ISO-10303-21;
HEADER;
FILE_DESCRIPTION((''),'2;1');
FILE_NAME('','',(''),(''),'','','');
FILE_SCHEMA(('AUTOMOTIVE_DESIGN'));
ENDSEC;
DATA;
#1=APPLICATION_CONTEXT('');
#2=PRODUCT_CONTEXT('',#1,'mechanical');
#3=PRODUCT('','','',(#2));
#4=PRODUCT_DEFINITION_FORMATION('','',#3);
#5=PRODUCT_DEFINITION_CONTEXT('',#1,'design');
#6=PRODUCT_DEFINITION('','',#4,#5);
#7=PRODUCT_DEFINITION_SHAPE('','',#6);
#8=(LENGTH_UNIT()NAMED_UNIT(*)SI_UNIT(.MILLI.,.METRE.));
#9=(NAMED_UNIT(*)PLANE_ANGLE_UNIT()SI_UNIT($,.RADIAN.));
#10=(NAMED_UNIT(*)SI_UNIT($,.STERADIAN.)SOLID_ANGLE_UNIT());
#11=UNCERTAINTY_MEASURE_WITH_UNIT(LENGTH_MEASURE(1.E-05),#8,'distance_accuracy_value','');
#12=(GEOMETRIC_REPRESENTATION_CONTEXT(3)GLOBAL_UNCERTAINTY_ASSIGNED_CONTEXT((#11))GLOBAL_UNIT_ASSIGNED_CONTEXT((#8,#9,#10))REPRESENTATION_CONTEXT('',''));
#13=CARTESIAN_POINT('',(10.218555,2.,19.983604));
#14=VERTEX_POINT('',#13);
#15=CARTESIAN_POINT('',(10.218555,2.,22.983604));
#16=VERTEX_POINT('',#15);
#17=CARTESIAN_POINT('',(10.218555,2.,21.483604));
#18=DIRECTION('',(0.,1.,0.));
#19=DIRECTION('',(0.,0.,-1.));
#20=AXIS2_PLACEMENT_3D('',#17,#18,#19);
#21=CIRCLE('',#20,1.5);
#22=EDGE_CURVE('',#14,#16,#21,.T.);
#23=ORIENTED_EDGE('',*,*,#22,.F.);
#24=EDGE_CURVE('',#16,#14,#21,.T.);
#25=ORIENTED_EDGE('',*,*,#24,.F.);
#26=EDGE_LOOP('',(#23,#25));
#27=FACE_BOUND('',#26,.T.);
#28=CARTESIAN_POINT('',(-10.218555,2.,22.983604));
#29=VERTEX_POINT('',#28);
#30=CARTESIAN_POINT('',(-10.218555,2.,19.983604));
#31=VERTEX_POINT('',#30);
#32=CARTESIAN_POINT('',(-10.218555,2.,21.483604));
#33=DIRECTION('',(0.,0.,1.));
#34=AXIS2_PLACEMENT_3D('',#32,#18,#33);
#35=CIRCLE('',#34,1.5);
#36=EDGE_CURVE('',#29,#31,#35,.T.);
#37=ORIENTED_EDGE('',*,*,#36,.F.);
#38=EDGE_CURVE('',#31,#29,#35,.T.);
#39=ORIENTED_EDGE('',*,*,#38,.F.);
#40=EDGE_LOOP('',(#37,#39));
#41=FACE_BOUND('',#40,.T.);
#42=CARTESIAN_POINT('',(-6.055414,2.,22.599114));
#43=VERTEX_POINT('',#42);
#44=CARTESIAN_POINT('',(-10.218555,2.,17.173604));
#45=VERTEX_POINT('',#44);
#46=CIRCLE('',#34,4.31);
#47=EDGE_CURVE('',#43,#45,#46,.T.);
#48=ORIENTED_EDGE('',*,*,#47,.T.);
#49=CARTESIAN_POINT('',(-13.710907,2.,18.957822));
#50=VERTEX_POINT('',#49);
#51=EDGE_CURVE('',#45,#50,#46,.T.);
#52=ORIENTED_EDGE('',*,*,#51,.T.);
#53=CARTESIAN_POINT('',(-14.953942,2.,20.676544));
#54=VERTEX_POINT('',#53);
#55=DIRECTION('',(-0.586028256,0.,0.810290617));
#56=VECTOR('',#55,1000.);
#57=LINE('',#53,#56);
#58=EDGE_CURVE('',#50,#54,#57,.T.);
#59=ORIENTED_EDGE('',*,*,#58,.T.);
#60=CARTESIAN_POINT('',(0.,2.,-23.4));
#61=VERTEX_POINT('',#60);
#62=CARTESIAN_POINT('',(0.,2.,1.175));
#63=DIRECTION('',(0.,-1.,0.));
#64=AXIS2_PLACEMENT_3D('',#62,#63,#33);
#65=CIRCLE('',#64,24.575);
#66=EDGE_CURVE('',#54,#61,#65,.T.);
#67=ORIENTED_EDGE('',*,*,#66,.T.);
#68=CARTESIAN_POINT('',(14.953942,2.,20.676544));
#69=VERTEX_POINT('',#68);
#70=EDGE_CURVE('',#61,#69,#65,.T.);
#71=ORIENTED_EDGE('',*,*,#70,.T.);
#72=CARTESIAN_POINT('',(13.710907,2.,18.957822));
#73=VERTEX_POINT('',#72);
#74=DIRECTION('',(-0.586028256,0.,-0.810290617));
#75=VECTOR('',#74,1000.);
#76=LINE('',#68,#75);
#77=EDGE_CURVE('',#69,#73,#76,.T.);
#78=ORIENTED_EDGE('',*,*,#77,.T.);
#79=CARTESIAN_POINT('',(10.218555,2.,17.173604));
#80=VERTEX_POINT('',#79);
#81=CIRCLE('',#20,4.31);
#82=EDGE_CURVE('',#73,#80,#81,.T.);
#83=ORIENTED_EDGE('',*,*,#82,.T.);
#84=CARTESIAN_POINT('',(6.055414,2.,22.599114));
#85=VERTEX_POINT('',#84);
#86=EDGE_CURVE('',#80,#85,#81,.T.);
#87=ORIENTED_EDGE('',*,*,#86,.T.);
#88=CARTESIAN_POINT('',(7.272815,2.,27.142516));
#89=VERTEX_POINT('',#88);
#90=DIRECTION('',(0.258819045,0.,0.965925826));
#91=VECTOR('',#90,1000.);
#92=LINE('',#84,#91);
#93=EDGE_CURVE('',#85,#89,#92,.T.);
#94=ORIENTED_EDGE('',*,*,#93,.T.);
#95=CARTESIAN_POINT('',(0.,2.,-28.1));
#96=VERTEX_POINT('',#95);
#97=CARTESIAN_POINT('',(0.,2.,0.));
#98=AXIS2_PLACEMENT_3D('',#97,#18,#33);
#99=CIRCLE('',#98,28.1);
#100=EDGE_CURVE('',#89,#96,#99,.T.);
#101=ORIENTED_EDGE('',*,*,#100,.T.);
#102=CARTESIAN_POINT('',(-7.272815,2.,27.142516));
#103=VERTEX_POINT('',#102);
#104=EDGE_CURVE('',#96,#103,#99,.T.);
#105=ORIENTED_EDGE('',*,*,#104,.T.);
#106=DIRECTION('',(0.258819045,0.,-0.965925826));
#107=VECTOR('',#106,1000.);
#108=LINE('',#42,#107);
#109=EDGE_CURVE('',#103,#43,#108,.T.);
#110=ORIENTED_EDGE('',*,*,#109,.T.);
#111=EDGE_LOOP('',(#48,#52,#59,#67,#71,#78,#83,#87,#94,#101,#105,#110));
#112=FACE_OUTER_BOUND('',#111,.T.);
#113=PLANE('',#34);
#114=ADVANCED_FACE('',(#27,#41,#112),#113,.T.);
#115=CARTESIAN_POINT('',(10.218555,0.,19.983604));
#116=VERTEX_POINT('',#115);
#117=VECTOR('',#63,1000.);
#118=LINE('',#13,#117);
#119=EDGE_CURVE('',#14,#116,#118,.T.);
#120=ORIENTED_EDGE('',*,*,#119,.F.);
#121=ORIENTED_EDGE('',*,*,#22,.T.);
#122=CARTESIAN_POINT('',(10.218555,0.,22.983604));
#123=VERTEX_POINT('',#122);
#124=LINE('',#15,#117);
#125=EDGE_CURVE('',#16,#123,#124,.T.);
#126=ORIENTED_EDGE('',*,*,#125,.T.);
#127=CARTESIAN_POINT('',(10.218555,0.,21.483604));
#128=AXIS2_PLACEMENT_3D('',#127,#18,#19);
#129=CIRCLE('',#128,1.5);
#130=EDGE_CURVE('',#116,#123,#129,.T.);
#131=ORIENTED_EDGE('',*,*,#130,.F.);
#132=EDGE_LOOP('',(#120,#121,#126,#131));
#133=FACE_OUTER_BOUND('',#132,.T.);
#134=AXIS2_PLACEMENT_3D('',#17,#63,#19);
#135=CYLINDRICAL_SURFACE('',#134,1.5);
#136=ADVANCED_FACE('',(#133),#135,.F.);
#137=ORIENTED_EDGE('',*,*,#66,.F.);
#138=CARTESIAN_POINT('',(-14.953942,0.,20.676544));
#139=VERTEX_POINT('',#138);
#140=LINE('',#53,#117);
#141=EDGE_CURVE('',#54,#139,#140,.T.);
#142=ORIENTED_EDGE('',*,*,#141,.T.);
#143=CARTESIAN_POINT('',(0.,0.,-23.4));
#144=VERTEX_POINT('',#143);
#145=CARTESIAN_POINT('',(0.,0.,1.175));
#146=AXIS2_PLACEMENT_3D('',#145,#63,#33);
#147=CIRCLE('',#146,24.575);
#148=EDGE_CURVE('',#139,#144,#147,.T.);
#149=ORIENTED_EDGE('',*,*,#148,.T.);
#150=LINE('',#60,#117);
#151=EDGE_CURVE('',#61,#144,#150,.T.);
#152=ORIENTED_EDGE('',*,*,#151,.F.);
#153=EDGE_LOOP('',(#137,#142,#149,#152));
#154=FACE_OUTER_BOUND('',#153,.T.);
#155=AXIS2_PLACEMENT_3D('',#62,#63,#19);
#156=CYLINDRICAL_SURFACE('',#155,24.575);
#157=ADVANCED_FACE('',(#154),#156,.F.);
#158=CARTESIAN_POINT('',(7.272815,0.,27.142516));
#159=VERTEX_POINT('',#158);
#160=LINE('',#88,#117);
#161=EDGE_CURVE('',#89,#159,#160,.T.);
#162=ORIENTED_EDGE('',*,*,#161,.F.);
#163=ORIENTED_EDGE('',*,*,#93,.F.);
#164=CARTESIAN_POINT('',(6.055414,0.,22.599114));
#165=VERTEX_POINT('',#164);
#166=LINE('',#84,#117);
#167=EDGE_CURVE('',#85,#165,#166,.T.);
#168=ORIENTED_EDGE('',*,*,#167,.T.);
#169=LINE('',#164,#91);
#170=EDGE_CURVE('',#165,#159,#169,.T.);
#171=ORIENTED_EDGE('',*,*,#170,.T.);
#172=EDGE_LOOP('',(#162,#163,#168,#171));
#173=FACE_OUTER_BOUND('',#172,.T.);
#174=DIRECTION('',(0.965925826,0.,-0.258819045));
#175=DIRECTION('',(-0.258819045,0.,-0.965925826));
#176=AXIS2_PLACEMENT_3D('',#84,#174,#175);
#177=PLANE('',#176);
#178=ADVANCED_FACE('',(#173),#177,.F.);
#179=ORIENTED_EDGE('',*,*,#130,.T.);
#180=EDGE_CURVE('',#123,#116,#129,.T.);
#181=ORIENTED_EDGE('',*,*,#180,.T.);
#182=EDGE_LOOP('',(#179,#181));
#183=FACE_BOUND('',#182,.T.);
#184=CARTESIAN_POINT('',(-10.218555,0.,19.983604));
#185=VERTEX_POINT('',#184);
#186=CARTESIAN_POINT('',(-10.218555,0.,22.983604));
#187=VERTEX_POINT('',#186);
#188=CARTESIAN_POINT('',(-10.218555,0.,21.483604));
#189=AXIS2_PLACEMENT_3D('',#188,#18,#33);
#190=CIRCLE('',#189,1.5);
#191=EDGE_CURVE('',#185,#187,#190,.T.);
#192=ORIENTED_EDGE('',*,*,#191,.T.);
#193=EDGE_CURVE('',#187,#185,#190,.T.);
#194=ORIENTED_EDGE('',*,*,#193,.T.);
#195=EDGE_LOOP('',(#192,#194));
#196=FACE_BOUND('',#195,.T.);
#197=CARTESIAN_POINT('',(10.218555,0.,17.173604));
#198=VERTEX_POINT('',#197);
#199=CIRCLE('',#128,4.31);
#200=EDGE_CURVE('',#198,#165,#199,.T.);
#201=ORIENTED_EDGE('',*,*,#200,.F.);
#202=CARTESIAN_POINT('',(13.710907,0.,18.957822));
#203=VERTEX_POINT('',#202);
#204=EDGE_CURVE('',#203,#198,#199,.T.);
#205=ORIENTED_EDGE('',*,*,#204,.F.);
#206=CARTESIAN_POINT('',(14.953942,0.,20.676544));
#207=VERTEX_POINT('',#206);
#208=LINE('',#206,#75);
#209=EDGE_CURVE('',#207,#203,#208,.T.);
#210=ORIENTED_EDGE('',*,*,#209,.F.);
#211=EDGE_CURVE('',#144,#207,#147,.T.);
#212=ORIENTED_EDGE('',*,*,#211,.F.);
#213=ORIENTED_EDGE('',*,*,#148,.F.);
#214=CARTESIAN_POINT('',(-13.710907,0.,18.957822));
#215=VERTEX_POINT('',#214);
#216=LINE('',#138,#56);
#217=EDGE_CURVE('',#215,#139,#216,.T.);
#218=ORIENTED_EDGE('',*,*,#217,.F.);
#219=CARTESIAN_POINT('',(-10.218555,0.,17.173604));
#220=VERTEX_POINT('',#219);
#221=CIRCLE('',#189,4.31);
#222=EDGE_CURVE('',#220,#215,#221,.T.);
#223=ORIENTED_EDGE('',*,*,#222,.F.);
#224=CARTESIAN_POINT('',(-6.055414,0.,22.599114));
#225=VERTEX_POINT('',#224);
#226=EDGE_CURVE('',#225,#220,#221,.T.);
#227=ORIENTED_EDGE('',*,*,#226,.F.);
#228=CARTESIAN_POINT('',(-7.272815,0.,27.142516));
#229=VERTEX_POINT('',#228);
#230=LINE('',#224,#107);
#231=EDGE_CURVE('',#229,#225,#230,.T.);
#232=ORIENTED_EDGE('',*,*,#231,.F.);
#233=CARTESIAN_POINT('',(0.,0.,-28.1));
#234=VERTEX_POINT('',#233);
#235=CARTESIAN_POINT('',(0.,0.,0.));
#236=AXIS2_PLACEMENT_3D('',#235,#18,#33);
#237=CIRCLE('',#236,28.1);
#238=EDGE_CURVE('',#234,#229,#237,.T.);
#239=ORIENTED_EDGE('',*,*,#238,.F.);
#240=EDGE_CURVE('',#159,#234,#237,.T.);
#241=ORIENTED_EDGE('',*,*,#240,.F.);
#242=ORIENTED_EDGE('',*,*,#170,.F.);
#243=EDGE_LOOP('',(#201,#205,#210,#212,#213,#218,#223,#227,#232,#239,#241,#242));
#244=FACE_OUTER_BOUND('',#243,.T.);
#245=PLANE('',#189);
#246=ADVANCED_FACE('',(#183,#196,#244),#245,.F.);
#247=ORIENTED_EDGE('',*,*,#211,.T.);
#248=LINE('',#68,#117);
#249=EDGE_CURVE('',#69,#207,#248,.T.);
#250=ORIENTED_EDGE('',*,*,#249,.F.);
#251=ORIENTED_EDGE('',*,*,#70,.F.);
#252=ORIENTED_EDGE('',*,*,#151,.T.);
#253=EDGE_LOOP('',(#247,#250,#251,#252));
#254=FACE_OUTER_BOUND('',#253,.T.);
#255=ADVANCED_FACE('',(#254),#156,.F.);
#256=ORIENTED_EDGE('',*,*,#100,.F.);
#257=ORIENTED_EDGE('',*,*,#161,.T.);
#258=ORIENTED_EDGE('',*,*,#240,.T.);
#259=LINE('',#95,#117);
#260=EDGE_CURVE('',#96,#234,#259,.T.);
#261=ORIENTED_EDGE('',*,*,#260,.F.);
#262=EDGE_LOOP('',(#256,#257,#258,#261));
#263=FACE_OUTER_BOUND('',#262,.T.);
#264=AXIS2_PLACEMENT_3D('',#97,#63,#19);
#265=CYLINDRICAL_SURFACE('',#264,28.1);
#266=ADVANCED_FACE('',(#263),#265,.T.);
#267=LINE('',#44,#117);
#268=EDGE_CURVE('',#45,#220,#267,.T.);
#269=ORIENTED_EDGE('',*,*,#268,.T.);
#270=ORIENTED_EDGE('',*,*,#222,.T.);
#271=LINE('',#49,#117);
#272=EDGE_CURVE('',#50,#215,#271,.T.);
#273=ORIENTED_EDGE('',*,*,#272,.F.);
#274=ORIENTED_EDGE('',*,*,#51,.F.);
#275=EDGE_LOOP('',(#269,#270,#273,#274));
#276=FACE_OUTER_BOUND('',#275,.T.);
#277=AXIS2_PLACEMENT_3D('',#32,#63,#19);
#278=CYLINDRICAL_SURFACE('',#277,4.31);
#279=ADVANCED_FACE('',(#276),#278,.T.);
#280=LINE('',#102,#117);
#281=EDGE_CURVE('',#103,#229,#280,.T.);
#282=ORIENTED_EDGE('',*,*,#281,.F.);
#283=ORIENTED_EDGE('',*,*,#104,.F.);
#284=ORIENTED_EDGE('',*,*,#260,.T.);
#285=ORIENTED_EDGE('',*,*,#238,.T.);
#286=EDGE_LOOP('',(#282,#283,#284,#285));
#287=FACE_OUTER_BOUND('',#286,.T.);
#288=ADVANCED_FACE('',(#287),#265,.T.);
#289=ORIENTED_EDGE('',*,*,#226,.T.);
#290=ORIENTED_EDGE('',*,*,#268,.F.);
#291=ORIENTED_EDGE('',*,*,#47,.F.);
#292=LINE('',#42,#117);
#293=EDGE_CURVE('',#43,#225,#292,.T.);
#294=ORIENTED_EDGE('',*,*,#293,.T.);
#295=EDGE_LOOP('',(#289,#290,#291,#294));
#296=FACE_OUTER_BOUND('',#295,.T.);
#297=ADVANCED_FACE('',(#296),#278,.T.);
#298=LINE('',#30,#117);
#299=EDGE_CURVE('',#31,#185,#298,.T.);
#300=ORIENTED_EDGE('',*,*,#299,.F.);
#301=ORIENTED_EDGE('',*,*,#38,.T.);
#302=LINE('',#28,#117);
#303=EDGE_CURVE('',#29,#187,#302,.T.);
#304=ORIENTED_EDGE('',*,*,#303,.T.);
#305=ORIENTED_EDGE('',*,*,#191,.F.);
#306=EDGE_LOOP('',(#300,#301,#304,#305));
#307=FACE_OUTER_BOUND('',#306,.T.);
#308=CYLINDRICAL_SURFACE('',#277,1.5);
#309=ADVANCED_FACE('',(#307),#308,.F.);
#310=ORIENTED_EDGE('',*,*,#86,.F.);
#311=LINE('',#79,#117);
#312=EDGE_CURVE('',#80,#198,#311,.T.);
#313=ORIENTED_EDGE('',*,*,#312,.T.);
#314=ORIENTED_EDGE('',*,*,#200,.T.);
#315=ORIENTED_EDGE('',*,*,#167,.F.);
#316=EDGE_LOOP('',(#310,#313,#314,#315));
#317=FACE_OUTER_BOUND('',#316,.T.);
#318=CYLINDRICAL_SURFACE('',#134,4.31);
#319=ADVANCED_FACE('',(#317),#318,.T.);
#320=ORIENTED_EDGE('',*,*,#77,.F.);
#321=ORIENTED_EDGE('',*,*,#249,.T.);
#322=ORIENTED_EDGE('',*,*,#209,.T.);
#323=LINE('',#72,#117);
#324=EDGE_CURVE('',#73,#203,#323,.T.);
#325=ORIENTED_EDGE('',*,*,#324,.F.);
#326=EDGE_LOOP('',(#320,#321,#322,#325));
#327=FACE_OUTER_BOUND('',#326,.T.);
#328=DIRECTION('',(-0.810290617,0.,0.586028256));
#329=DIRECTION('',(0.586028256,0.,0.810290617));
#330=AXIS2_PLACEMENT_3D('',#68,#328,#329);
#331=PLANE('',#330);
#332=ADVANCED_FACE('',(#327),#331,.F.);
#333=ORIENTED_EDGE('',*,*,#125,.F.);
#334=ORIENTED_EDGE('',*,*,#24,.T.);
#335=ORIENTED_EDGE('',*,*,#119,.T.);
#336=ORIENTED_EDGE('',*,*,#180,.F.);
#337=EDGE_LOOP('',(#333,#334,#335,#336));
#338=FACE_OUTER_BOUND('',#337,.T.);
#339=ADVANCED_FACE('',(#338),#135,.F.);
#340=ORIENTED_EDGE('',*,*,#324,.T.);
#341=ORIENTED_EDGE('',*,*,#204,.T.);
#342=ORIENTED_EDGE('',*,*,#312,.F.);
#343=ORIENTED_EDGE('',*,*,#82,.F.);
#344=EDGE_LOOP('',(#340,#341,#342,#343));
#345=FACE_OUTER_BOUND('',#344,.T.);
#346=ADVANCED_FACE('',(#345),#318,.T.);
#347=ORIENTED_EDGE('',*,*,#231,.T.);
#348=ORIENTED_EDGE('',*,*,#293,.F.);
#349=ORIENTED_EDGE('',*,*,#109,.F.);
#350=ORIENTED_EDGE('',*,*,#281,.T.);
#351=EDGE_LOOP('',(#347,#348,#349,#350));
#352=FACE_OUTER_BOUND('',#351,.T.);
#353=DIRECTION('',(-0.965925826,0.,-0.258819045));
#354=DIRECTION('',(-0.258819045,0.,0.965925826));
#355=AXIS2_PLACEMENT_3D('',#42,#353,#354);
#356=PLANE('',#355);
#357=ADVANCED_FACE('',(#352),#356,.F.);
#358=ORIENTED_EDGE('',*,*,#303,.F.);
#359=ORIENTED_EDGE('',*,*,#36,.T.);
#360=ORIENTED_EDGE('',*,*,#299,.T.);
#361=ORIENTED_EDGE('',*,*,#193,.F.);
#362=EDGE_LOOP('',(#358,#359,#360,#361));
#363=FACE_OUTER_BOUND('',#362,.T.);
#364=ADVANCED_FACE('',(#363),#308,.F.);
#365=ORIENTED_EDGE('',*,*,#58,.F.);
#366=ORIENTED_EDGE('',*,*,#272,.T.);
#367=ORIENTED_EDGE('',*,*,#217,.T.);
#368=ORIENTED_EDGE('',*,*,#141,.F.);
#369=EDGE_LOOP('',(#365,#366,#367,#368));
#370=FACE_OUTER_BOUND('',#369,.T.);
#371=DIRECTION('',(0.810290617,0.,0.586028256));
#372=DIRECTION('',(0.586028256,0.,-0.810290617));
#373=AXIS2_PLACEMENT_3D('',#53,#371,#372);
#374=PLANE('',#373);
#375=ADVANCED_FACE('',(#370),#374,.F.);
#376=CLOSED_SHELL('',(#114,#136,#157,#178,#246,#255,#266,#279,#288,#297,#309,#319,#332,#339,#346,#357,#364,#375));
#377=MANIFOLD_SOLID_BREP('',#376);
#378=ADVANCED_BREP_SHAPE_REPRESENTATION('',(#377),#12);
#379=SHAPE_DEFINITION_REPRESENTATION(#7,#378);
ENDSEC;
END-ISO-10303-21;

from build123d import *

# Parameters (mm, degrees)
SKETCH2_R           = 1.5
BOSS_EXTRUDE1_DEPTH = 2


with BuildPart() as part:
    # Sketch2 → Boss-Extrude1 (new body)
    with BuildSketch(Plane(origin=(0, 0, 0), x_dir=(1, 0, 0), z_dir=(0, 1, 0))):
        with BuildLine():
            Line((-14.953942403, -20.676544339), (-13.710907235, -18.957822206))
            ThreePointArc((-13.710907235, -18.957822206), (-8.367273859, -17.591450428), (-6.055414365, -22.599114073))
            Line((-6.055414365, -22.599114073), (-7.272815167, -27.142515719))
            ThreePointArc((-7.272815167, -27.142515719), (0, 28.1), (7.272815167, -27.142515719))
            Line((7.272815167, -27.142515719), (6.055414365, -22.599114073))
            ThreePointArc((6.055414365, -22.599114073), (8.367273859, -17.591450428), (13.710907235, -18.957822206))
            Line((13.710907235, -18.957822206), (14.953942403, -20.676544339))
            ThreePointArc((14.953942403, -20.676544339), (0, 23.4), (-14.953942403, -20.676544339))
        make_face()
        with Locations(Location((-10.218554677, -21.483603988, 0), (0, 0, 270))):
            Circle(SKETCH2_R, mode=Mode.SUBTRACT)
        with Locations(Location((10.218554677, -21.483603988, 0), (0, 0, 90))):
            Circle(SKETCH2_R, mode=Mode.SUBTRACT)
    extrude(amount=BOSS_EXTRUDE1_DEPTH)


solid = part.part
